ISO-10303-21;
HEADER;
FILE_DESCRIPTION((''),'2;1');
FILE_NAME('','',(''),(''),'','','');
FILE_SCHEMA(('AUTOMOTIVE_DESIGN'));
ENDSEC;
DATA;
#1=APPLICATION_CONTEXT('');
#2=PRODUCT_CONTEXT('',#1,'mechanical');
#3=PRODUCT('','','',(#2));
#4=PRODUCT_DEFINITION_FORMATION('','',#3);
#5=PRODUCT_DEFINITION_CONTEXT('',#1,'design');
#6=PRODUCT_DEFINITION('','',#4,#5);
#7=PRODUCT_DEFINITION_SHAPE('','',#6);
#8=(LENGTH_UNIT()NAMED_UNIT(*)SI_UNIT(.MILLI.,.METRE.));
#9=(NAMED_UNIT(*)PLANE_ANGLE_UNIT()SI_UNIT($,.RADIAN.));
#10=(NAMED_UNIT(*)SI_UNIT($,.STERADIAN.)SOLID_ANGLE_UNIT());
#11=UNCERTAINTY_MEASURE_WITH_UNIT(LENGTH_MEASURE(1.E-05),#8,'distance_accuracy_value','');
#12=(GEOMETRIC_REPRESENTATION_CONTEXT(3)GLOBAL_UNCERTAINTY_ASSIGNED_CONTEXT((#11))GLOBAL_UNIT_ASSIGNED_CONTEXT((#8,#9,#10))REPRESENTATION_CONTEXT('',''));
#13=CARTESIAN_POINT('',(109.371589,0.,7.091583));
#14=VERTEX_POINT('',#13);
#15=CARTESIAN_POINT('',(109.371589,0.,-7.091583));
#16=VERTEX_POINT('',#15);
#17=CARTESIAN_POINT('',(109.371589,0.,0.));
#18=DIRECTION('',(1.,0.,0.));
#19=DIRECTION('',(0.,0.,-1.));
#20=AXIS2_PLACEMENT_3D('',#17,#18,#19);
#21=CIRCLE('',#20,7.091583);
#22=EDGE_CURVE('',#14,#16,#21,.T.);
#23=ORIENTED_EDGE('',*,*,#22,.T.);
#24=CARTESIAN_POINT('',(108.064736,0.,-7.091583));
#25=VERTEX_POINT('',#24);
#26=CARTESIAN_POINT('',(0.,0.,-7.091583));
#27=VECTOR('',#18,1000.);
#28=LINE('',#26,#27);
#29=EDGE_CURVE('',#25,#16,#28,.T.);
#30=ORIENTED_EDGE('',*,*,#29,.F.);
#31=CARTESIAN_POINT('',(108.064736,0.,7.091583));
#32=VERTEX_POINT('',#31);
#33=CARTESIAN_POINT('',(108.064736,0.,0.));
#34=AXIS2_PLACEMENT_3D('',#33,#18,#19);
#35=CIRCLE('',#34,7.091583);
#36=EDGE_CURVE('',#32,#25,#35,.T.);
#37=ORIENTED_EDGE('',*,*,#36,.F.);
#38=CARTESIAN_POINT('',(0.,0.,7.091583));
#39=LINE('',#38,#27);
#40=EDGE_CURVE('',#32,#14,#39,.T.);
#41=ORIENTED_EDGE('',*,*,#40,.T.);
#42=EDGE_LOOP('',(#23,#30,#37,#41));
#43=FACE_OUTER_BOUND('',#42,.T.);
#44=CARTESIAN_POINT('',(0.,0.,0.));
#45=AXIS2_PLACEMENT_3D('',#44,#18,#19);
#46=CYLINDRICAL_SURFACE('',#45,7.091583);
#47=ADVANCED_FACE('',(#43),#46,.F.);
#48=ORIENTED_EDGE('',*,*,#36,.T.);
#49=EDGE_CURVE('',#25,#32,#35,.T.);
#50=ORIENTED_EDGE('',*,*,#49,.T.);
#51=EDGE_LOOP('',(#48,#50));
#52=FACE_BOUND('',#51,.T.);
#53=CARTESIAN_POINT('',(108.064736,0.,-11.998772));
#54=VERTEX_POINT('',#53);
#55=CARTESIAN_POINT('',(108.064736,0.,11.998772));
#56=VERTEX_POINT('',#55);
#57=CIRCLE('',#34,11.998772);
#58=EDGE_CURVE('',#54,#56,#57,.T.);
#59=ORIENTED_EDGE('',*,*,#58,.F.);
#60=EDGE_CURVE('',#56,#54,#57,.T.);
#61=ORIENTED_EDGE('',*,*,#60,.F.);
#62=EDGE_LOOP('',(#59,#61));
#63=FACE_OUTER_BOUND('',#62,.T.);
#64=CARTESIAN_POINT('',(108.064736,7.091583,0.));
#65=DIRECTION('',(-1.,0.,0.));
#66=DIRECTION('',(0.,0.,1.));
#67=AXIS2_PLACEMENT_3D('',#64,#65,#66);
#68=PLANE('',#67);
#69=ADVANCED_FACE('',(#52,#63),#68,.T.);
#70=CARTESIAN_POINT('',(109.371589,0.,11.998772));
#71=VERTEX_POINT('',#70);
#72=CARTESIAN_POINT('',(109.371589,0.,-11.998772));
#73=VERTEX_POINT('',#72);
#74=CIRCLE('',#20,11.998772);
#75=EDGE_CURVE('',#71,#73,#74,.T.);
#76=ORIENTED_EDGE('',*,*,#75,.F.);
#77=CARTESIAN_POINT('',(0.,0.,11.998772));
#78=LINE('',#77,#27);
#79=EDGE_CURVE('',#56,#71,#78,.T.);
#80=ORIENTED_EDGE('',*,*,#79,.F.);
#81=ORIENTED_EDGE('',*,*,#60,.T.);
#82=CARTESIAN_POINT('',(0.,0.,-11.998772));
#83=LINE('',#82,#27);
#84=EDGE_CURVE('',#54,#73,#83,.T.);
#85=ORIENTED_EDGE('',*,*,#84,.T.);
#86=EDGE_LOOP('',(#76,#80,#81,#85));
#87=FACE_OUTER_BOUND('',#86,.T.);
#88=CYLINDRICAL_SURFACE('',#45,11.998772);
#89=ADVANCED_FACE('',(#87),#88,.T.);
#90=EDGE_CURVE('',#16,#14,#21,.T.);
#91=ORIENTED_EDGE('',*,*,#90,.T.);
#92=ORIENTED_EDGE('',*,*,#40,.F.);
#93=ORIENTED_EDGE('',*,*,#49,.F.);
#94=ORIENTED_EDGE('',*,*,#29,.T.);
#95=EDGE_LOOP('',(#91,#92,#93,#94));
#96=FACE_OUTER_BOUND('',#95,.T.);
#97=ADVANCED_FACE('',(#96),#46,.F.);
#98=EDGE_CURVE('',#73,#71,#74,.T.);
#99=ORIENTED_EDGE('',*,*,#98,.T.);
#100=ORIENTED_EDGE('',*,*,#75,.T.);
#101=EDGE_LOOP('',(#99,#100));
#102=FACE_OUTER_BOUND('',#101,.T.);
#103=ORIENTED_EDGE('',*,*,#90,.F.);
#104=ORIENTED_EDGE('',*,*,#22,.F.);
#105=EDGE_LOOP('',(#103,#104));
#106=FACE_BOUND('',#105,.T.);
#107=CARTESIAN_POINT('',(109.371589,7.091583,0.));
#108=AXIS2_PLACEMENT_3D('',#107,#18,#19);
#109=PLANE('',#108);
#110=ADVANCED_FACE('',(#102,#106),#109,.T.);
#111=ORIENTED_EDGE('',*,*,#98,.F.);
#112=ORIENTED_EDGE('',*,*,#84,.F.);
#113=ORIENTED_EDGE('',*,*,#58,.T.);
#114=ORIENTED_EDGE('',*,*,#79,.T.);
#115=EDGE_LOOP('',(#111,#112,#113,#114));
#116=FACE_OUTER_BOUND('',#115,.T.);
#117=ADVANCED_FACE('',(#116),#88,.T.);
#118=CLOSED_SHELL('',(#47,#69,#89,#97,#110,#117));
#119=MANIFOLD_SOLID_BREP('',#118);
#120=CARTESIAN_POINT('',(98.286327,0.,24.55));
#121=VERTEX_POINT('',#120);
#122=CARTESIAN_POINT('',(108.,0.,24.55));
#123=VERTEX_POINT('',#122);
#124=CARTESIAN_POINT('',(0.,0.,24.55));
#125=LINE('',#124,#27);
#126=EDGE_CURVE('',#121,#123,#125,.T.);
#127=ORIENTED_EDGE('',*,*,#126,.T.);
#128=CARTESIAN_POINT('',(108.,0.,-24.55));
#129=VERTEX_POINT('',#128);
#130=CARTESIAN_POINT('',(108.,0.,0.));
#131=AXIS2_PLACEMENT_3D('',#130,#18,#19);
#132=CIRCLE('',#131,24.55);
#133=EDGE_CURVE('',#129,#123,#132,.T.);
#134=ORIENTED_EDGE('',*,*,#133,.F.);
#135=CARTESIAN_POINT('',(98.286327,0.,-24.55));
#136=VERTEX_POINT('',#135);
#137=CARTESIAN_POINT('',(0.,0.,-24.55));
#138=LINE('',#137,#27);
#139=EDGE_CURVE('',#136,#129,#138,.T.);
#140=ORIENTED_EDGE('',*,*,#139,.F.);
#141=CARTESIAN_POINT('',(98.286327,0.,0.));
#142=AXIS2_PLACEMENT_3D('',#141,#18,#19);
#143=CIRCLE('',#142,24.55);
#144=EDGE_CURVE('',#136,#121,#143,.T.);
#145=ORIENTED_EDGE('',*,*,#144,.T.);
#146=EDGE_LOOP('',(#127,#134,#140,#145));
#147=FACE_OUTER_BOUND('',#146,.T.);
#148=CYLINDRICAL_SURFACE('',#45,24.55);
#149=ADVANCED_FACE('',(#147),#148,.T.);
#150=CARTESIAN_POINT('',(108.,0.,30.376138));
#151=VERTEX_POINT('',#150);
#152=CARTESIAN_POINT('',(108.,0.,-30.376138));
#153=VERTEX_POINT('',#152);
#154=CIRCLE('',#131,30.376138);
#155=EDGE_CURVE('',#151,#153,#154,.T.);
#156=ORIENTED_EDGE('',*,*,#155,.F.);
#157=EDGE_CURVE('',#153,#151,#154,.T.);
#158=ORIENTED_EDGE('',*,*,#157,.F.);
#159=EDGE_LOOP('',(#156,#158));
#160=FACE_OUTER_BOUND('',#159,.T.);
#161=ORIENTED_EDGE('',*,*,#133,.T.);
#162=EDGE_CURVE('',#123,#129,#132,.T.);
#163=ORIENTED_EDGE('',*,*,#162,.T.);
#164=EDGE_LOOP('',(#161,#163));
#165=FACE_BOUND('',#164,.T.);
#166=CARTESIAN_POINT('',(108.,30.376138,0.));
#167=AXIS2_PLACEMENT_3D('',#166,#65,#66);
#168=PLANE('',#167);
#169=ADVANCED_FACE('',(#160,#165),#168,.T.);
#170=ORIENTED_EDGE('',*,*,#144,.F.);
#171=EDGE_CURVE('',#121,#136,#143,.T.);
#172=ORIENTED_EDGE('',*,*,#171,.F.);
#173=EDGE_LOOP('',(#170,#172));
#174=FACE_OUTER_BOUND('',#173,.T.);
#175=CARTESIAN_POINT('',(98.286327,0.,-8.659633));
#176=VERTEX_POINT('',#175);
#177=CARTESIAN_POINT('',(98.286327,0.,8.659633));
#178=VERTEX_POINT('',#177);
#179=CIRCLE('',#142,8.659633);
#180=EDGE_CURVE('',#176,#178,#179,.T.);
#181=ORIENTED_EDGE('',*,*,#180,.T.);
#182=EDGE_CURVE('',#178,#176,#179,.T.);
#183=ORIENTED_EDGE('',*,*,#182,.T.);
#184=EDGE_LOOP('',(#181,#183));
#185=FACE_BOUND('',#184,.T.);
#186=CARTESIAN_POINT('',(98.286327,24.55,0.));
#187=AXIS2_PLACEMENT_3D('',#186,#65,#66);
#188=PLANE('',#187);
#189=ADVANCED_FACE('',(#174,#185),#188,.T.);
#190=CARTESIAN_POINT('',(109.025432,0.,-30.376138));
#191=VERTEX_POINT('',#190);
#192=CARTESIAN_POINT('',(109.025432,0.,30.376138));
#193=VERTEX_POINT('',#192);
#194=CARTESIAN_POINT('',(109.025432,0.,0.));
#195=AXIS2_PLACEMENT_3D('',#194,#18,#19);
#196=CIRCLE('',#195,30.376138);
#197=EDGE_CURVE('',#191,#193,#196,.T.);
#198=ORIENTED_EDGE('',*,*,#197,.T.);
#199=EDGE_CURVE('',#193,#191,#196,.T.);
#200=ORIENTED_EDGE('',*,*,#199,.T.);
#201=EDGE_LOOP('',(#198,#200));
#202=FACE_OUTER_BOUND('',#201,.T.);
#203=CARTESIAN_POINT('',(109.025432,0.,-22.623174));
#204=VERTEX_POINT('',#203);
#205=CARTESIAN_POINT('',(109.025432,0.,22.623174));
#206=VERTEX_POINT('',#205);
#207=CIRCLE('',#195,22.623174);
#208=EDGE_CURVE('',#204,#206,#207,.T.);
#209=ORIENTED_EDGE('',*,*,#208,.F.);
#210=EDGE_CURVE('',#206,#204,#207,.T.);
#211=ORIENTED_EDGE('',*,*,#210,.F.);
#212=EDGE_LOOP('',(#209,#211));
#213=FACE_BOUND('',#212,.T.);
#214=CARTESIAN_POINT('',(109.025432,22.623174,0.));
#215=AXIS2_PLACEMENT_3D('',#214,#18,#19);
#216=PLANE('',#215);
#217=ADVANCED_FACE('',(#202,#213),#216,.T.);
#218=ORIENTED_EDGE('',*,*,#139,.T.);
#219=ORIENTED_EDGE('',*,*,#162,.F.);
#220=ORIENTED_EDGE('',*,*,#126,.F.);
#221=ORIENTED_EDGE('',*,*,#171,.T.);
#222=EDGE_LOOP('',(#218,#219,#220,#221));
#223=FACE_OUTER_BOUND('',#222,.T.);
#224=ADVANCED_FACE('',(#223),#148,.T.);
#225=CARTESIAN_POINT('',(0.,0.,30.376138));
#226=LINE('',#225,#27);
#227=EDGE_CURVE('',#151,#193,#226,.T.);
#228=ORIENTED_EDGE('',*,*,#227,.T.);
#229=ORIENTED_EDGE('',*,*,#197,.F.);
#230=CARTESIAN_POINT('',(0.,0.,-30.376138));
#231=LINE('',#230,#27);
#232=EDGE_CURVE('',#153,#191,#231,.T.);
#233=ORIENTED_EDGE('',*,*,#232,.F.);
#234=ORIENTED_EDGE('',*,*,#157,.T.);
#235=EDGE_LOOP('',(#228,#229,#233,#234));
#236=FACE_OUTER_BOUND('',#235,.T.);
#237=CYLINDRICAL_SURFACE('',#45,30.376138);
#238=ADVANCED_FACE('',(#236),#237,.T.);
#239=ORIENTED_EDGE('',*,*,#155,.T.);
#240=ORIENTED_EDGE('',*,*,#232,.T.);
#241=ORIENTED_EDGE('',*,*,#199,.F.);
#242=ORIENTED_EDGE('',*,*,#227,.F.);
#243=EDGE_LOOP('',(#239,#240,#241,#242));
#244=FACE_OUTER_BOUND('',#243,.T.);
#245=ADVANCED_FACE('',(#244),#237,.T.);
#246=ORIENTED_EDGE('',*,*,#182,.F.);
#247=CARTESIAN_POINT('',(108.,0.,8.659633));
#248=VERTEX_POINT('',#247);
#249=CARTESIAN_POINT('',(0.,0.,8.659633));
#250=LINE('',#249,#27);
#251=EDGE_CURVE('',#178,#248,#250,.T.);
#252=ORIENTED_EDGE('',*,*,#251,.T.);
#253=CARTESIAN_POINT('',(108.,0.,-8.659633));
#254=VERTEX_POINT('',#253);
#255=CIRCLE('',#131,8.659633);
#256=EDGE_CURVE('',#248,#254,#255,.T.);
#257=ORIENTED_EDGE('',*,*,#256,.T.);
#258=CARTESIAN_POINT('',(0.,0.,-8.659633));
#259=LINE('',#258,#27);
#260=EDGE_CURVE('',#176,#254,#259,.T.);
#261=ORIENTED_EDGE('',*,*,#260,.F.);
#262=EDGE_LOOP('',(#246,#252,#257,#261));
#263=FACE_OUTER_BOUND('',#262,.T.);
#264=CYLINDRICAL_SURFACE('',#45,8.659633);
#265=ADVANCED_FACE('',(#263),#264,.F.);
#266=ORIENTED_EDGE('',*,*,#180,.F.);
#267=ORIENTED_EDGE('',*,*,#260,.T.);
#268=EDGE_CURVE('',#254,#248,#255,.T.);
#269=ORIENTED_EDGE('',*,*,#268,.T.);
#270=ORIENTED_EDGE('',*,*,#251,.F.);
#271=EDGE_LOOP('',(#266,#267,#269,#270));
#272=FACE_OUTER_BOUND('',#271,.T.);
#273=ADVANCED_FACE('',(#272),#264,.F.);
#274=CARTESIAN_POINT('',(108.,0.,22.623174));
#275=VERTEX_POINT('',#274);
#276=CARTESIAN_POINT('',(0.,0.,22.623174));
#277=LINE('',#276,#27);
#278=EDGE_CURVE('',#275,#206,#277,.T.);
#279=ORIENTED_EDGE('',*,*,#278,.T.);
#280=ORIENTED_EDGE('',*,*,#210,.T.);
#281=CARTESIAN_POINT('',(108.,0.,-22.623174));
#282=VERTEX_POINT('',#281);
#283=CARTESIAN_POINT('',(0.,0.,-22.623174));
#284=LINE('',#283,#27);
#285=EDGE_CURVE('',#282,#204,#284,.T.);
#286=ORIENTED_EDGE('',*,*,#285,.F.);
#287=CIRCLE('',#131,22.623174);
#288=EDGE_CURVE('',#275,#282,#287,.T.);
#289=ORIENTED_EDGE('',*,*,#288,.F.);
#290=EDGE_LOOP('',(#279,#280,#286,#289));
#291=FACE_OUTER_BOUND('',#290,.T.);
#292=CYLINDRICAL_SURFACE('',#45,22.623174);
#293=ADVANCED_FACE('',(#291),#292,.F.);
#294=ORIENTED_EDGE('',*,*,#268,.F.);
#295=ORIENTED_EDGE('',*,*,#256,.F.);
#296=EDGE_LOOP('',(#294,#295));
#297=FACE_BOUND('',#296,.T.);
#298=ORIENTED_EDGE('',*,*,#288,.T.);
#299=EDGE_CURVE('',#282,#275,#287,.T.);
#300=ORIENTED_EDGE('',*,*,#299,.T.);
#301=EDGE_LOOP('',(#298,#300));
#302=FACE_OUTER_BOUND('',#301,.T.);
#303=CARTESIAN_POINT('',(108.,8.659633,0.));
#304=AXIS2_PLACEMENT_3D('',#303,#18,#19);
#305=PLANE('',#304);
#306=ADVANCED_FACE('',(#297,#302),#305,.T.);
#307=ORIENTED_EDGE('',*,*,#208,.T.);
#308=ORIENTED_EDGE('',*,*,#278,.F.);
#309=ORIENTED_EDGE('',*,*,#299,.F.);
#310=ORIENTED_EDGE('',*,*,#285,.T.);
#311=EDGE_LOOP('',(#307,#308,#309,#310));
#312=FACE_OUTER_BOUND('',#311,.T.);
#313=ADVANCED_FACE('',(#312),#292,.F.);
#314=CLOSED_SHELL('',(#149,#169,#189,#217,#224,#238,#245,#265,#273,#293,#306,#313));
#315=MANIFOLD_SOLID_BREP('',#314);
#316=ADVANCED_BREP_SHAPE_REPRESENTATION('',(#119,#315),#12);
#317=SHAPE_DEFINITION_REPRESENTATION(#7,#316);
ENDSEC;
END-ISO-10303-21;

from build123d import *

# Parameters (mm, degrees)
SKETCH1_W = 1.306852865
SKETCH1_H = 4.907189237


with BuildPart() as part:
    # Sketch1 → Revolve1 (revolve)
    with BuildSketch(Plane.XY, mode=Mode.PRIVATE) as revolve1_sk:
        Polygon((108, 30.376137781), (108, 24.55), (98.286326817, 24.55), (98.286326817, 8.659632807), (108, 8.659632807), (108, 22.623174238), (109.025432246, 22.623174238), (109.025432246, 30.376137781), align=None)
        with Locations((108.718162295, 9.545177183)):
            Rectangle(SKETCH1_W, SKETCH1_H)
    revolve(revolve1_sk.sketch.rotate(Axis((0, 0, 0), (-1, 0, 0)), 90), axis=Axis((0, 0, 0), (-1, 0, 0)))


solid = part.part
